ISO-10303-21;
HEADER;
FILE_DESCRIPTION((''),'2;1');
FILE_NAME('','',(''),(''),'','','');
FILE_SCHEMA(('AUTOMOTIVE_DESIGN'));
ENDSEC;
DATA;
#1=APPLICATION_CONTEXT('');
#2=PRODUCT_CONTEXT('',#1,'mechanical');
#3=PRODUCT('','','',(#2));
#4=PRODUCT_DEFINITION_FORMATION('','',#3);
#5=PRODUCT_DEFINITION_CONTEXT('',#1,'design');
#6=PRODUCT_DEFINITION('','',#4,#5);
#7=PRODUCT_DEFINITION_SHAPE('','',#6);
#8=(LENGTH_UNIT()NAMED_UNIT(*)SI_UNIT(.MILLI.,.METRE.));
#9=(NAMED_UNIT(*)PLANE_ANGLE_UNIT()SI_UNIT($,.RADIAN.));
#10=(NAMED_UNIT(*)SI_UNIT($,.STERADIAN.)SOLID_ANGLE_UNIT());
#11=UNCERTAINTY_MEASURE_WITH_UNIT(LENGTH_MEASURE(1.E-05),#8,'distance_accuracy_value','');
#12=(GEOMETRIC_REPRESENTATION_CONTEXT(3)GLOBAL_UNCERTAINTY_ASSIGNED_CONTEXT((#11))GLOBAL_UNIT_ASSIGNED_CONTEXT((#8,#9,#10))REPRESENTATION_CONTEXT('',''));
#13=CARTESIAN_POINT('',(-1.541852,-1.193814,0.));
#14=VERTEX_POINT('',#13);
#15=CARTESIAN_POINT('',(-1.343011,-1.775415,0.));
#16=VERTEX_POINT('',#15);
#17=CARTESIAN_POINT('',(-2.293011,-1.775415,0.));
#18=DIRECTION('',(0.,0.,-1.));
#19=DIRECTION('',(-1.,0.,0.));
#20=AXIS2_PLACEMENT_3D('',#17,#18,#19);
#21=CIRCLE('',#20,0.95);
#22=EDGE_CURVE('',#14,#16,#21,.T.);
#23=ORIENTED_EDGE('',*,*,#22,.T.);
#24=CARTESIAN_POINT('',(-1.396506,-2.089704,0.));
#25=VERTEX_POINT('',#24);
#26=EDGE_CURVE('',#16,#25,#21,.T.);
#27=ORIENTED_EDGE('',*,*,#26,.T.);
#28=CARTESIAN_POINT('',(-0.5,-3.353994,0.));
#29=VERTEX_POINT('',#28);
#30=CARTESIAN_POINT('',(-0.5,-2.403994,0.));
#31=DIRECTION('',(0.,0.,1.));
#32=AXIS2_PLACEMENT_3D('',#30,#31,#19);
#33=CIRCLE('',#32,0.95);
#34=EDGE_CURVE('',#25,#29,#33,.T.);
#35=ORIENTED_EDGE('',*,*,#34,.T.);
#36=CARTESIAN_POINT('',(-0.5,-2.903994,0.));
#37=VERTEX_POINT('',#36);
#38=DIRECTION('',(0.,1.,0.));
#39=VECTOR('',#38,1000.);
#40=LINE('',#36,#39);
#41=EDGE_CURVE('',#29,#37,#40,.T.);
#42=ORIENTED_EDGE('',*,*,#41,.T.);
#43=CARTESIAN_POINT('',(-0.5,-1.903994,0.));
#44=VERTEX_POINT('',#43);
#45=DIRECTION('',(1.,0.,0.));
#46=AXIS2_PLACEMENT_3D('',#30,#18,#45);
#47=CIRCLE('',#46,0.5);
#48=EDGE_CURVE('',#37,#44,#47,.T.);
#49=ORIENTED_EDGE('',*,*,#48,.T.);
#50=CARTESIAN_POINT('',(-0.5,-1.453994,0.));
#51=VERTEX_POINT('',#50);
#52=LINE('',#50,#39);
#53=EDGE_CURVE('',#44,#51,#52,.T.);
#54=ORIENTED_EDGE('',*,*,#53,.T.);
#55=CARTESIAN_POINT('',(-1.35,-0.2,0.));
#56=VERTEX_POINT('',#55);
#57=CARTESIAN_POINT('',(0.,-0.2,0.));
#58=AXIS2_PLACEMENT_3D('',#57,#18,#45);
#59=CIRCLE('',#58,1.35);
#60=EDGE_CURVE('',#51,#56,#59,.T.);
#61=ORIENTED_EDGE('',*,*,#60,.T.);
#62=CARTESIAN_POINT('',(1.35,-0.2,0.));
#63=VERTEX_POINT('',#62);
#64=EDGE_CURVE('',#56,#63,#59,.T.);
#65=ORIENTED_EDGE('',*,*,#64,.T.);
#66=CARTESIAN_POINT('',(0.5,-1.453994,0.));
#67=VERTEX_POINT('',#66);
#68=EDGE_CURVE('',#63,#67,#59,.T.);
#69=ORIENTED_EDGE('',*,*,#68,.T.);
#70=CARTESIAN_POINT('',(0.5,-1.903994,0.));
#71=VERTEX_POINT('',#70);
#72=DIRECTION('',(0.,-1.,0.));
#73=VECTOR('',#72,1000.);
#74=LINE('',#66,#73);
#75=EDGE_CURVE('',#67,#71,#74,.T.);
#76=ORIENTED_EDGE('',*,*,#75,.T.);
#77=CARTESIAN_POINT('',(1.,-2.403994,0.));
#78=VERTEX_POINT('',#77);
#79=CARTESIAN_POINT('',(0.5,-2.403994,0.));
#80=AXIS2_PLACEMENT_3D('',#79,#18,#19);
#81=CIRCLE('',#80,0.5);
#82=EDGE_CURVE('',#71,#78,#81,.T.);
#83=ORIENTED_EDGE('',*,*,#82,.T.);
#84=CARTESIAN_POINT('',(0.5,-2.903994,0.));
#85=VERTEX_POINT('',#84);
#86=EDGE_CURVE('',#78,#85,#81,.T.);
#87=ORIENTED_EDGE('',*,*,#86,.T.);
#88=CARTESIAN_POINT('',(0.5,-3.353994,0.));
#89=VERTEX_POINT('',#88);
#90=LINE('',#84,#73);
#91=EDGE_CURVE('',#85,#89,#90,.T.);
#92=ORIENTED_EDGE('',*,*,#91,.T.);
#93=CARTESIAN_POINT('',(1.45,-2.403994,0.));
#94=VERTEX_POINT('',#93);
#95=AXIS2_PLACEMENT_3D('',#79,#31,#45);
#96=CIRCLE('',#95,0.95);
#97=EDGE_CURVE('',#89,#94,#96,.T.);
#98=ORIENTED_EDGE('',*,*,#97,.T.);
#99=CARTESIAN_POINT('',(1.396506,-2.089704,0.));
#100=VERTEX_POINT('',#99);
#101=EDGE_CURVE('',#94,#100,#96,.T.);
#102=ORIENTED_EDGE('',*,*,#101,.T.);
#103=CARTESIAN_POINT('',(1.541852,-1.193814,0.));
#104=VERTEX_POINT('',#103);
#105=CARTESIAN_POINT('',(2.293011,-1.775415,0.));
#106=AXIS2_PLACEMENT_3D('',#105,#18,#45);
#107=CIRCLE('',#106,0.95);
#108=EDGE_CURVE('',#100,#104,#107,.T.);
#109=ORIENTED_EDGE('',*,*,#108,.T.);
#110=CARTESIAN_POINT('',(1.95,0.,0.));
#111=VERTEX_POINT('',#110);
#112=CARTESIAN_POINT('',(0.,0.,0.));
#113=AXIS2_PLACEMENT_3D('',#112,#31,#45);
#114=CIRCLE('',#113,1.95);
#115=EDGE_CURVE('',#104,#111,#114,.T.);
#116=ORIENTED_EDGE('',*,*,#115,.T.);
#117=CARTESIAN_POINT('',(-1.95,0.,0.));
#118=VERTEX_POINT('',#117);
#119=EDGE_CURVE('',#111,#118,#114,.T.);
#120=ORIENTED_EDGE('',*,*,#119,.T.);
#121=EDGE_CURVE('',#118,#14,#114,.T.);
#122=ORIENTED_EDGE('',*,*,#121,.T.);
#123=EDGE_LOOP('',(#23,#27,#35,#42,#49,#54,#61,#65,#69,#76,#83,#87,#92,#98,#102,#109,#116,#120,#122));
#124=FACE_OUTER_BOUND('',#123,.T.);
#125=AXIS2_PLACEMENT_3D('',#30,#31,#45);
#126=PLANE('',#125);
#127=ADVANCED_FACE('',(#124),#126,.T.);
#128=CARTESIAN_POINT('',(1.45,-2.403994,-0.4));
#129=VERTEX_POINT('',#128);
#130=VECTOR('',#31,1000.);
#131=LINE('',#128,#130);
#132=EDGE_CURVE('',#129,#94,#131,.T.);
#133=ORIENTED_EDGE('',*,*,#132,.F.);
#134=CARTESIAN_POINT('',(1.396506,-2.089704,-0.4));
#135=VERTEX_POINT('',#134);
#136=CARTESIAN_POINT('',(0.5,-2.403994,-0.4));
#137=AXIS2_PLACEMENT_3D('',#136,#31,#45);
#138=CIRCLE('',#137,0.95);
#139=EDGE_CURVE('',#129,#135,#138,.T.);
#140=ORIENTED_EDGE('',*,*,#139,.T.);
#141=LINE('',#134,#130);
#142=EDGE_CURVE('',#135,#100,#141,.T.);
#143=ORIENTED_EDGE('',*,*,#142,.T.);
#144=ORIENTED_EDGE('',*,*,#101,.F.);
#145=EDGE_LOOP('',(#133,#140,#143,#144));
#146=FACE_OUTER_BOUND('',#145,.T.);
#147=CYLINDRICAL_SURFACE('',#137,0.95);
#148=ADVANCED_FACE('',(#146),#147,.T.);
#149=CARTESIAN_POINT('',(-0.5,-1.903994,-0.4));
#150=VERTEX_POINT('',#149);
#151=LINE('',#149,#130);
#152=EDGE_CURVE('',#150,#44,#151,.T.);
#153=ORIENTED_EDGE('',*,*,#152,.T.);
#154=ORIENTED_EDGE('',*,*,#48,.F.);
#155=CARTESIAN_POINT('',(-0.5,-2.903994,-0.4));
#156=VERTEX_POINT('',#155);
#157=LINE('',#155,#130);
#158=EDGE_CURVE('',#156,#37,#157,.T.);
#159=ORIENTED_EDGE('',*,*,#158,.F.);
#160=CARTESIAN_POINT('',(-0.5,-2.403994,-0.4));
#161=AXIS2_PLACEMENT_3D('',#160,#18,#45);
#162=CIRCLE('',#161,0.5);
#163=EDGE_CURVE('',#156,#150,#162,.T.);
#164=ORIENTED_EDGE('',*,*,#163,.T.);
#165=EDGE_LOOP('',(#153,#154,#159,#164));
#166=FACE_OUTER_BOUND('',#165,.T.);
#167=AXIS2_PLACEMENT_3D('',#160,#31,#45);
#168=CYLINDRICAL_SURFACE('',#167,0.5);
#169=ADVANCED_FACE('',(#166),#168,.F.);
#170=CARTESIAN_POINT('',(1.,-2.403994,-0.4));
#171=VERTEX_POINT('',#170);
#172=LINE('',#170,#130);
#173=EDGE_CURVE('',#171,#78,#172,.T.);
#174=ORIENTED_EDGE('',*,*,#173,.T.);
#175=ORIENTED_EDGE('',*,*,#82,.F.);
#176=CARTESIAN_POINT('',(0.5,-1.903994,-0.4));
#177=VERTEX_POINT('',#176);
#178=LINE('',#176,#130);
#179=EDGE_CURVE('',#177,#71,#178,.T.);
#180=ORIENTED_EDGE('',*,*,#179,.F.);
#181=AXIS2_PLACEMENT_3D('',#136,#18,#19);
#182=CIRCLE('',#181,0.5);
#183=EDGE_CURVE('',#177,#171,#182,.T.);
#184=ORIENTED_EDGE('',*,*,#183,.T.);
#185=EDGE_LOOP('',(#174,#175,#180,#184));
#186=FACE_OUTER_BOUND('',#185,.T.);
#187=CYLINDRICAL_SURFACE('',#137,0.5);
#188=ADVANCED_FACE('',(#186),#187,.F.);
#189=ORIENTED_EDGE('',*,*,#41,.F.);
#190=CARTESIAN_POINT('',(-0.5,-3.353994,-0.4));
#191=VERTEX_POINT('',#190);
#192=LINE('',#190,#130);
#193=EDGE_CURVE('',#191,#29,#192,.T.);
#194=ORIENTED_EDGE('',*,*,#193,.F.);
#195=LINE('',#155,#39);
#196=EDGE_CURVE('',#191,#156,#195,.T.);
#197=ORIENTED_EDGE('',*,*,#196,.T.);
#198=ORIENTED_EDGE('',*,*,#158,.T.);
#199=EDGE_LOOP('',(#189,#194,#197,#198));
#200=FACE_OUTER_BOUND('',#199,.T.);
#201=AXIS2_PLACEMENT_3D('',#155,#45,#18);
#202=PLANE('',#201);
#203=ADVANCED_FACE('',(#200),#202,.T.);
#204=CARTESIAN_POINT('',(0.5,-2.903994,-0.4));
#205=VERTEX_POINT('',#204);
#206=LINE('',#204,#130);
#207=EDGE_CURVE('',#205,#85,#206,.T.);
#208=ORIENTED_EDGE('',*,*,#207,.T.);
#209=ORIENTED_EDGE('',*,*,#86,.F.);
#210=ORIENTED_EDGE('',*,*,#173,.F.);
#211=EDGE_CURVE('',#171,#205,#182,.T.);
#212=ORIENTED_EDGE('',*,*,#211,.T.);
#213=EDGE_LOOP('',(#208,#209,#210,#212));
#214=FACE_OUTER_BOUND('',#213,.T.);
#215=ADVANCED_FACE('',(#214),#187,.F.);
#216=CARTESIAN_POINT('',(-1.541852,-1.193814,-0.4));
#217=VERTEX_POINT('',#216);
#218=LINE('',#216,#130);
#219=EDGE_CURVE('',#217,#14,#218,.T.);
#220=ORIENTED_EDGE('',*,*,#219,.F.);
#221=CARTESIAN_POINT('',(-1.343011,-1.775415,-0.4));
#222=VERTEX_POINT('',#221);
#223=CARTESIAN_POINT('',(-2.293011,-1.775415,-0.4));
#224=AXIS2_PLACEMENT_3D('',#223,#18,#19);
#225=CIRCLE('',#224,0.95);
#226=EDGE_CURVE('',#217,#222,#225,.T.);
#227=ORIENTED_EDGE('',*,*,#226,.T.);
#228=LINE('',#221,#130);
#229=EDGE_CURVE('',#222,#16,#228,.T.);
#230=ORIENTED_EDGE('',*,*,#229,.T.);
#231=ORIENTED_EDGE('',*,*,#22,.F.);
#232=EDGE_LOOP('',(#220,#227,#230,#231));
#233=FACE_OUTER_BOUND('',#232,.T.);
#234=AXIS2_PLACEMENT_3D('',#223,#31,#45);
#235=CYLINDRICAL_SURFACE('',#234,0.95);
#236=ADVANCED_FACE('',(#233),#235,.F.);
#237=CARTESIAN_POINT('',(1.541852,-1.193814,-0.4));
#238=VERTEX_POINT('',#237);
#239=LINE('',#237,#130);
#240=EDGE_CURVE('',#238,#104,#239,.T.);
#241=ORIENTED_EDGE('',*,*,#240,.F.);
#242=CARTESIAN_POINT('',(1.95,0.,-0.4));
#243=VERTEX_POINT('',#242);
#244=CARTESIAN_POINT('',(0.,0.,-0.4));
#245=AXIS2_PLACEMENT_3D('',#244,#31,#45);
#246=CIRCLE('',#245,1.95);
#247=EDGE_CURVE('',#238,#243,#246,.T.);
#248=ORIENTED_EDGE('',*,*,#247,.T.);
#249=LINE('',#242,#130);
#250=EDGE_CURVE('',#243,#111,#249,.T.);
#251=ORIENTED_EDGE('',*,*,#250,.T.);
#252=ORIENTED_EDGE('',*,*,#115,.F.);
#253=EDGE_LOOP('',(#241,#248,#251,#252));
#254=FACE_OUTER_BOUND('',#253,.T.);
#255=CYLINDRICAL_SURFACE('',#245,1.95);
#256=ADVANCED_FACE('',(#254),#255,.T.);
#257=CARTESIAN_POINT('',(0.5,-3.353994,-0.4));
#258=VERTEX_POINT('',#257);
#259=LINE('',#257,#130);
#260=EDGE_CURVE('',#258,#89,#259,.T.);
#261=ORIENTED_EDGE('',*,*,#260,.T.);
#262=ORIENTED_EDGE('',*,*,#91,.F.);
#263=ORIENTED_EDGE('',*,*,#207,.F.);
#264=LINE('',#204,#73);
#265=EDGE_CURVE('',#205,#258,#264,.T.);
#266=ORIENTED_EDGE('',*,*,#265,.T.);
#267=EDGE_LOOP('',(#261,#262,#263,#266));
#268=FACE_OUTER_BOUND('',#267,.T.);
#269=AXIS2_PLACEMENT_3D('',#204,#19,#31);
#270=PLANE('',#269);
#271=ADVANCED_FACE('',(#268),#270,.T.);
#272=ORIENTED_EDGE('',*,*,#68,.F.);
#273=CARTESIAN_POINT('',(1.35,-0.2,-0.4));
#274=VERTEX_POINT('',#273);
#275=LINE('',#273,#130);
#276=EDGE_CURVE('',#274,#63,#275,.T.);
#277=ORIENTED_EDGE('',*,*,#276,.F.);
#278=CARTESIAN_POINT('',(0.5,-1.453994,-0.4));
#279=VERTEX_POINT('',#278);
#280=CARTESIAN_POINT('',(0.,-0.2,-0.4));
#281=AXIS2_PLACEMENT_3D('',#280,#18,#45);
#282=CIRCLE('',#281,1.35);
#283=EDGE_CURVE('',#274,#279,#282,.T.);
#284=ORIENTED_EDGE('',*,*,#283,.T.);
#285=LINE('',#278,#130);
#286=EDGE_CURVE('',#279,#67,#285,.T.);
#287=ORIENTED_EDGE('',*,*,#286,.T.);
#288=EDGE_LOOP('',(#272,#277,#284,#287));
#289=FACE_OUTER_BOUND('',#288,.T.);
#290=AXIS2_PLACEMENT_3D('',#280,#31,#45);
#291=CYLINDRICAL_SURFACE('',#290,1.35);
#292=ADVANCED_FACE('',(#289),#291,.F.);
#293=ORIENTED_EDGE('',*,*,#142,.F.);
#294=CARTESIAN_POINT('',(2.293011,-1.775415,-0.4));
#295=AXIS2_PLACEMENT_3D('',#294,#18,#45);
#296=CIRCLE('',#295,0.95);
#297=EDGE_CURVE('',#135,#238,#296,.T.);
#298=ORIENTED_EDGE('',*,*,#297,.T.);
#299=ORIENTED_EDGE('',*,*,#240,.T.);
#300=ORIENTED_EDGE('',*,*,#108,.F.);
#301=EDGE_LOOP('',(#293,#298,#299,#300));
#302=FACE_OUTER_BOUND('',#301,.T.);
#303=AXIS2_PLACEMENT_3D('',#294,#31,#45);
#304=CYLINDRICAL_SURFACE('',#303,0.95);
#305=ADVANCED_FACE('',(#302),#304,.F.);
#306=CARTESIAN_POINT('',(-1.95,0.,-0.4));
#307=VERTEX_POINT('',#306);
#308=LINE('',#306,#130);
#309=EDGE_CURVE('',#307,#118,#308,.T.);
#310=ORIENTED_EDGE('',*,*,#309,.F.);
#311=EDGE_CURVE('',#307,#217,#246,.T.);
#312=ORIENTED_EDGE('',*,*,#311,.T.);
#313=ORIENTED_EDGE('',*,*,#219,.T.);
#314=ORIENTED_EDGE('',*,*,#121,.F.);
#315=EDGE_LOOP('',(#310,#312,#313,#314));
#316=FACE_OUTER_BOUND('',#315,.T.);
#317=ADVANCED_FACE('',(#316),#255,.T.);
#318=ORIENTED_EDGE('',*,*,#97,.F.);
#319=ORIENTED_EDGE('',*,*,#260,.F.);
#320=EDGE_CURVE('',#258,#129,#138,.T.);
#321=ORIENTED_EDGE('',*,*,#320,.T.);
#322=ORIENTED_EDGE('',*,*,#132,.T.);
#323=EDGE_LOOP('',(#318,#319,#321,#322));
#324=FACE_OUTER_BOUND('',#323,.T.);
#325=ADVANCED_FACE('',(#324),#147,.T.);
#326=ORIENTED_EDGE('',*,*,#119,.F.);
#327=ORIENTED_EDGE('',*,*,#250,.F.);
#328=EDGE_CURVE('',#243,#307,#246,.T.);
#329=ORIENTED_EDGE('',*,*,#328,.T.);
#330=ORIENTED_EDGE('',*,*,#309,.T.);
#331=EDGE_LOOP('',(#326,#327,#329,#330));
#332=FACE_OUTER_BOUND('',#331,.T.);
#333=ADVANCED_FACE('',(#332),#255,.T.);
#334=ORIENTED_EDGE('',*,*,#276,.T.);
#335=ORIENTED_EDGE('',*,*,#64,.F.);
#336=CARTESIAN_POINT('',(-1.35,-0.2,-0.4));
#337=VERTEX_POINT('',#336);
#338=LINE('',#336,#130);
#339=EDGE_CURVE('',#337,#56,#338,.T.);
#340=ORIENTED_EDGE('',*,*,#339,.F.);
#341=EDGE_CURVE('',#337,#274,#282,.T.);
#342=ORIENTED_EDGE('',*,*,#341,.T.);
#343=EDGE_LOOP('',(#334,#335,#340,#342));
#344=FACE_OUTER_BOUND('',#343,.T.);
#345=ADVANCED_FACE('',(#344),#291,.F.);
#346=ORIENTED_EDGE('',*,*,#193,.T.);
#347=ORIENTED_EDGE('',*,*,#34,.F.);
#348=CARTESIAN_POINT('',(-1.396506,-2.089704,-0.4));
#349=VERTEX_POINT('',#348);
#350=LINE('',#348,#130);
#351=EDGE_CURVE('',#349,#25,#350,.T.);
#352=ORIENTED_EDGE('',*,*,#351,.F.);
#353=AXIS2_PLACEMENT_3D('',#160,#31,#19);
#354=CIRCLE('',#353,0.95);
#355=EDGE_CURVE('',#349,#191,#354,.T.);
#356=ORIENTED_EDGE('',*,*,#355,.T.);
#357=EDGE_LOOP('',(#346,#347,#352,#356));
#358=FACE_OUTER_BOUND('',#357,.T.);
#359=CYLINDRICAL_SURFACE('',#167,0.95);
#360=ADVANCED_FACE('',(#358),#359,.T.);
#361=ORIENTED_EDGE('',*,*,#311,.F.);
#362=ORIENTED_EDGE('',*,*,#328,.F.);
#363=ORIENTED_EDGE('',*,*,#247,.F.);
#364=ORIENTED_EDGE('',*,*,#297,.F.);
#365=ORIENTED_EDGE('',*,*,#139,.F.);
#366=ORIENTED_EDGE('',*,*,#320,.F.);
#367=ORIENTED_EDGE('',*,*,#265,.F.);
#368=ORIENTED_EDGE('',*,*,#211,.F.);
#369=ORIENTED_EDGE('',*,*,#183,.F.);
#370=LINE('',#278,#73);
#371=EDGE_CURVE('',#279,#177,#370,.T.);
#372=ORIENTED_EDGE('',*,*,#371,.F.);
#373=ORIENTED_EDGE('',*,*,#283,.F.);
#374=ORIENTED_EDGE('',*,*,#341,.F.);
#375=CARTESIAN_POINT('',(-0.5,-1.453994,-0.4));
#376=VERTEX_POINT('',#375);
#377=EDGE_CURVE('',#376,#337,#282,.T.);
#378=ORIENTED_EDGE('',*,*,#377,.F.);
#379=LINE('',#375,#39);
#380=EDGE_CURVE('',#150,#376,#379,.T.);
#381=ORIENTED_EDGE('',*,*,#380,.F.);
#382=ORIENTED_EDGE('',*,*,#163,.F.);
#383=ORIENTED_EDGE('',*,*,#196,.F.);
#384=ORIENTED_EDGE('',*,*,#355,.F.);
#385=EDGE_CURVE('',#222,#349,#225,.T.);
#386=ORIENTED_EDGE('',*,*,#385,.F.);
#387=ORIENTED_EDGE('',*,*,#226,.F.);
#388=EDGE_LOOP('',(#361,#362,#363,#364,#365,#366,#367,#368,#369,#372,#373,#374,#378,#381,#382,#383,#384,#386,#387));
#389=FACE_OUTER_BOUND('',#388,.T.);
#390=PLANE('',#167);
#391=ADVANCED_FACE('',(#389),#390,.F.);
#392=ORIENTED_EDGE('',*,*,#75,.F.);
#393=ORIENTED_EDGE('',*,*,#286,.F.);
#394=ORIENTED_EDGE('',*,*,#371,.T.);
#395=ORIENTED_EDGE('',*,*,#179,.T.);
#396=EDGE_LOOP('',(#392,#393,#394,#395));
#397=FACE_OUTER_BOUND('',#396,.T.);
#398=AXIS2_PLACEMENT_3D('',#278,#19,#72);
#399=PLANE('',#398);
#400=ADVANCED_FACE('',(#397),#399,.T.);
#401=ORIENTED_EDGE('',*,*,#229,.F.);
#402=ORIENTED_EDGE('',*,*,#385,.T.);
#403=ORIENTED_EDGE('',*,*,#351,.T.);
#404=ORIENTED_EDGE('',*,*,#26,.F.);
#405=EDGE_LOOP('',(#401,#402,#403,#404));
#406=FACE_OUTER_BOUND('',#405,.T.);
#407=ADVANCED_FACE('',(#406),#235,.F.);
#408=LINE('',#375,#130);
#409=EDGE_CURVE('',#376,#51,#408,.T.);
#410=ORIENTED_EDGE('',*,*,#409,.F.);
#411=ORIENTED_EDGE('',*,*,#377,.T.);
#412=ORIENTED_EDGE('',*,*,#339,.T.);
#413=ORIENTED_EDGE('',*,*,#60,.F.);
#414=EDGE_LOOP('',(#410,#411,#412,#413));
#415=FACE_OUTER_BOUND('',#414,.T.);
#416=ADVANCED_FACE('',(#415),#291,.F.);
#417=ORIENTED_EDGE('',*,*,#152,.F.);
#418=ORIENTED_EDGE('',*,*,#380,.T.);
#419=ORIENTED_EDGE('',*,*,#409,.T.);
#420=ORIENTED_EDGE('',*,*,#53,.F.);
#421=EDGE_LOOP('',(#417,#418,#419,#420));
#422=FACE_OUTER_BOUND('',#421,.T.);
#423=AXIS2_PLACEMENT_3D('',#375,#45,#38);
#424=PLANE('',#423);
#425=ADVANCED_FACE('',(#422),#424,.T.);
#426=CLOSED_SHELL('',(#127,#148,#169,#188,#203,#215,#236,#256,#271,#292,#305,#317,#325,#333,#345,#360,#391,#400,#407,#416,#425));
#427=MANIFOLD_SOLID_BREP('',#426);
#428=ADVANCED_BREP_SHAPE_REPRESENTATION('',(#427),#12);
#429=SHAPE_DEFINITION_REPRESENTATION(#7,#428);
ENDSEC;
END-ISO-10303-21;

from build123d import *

# Parameters (mm, degrees)
BODY_DEPTH = 0.4


with BuildPart() as part:
    # Sketch1 → Body (new body)
    with BuildSketch(Plane.XY):
        with BuildLine():
            Line((-0.5, -1.45399362), (-0.5, -1.90399362))
            ThreePointArc((-0.5, -1.90399362), (-1, -2.40399362), (-0.5, -2.90399362))
            Line((-0.5, -2.90399362), (-0.5, -3.35399362))
            ThreePointArc((-0.5, -3.35399362), (-1.274943451, -2.953504901), (-1.396505618, -2.089704458))
            ThreePointArc((-1.396505618, -2.089704458), (-1.355272146, -1.623279172), (-1.541852382, -1.193813734))
            ThreePointArc((-1.541852382, -1.193813734), (0, 1.95), (1.541852382, -1.193813734))
            ThreePointArc((1.541852382, -1.193813734), (1.355272146, -1.623279172), (1.396505618, -2.089704458))
            ThreePointArc((1.396505618, -2.089704458), (1.274943451, -2.953504901), (0.5, -3.35399362))
            Line((0.5, -3.35399362), (0.5, -2.90399362))
            ThreePointArc((0.5, -2.90399362), (1, -2.40399362), (0.5, -1.90399362))
            Line((0.5, -1.90399362), (0.5, -1.45399362))
            ThreePointArc((0.5, -1.45399362), (0, 1.15), (-0.5, -1.45399362))
        make_face()
    extrude(amount=-BODY_DEPTH)


solid = part.part
